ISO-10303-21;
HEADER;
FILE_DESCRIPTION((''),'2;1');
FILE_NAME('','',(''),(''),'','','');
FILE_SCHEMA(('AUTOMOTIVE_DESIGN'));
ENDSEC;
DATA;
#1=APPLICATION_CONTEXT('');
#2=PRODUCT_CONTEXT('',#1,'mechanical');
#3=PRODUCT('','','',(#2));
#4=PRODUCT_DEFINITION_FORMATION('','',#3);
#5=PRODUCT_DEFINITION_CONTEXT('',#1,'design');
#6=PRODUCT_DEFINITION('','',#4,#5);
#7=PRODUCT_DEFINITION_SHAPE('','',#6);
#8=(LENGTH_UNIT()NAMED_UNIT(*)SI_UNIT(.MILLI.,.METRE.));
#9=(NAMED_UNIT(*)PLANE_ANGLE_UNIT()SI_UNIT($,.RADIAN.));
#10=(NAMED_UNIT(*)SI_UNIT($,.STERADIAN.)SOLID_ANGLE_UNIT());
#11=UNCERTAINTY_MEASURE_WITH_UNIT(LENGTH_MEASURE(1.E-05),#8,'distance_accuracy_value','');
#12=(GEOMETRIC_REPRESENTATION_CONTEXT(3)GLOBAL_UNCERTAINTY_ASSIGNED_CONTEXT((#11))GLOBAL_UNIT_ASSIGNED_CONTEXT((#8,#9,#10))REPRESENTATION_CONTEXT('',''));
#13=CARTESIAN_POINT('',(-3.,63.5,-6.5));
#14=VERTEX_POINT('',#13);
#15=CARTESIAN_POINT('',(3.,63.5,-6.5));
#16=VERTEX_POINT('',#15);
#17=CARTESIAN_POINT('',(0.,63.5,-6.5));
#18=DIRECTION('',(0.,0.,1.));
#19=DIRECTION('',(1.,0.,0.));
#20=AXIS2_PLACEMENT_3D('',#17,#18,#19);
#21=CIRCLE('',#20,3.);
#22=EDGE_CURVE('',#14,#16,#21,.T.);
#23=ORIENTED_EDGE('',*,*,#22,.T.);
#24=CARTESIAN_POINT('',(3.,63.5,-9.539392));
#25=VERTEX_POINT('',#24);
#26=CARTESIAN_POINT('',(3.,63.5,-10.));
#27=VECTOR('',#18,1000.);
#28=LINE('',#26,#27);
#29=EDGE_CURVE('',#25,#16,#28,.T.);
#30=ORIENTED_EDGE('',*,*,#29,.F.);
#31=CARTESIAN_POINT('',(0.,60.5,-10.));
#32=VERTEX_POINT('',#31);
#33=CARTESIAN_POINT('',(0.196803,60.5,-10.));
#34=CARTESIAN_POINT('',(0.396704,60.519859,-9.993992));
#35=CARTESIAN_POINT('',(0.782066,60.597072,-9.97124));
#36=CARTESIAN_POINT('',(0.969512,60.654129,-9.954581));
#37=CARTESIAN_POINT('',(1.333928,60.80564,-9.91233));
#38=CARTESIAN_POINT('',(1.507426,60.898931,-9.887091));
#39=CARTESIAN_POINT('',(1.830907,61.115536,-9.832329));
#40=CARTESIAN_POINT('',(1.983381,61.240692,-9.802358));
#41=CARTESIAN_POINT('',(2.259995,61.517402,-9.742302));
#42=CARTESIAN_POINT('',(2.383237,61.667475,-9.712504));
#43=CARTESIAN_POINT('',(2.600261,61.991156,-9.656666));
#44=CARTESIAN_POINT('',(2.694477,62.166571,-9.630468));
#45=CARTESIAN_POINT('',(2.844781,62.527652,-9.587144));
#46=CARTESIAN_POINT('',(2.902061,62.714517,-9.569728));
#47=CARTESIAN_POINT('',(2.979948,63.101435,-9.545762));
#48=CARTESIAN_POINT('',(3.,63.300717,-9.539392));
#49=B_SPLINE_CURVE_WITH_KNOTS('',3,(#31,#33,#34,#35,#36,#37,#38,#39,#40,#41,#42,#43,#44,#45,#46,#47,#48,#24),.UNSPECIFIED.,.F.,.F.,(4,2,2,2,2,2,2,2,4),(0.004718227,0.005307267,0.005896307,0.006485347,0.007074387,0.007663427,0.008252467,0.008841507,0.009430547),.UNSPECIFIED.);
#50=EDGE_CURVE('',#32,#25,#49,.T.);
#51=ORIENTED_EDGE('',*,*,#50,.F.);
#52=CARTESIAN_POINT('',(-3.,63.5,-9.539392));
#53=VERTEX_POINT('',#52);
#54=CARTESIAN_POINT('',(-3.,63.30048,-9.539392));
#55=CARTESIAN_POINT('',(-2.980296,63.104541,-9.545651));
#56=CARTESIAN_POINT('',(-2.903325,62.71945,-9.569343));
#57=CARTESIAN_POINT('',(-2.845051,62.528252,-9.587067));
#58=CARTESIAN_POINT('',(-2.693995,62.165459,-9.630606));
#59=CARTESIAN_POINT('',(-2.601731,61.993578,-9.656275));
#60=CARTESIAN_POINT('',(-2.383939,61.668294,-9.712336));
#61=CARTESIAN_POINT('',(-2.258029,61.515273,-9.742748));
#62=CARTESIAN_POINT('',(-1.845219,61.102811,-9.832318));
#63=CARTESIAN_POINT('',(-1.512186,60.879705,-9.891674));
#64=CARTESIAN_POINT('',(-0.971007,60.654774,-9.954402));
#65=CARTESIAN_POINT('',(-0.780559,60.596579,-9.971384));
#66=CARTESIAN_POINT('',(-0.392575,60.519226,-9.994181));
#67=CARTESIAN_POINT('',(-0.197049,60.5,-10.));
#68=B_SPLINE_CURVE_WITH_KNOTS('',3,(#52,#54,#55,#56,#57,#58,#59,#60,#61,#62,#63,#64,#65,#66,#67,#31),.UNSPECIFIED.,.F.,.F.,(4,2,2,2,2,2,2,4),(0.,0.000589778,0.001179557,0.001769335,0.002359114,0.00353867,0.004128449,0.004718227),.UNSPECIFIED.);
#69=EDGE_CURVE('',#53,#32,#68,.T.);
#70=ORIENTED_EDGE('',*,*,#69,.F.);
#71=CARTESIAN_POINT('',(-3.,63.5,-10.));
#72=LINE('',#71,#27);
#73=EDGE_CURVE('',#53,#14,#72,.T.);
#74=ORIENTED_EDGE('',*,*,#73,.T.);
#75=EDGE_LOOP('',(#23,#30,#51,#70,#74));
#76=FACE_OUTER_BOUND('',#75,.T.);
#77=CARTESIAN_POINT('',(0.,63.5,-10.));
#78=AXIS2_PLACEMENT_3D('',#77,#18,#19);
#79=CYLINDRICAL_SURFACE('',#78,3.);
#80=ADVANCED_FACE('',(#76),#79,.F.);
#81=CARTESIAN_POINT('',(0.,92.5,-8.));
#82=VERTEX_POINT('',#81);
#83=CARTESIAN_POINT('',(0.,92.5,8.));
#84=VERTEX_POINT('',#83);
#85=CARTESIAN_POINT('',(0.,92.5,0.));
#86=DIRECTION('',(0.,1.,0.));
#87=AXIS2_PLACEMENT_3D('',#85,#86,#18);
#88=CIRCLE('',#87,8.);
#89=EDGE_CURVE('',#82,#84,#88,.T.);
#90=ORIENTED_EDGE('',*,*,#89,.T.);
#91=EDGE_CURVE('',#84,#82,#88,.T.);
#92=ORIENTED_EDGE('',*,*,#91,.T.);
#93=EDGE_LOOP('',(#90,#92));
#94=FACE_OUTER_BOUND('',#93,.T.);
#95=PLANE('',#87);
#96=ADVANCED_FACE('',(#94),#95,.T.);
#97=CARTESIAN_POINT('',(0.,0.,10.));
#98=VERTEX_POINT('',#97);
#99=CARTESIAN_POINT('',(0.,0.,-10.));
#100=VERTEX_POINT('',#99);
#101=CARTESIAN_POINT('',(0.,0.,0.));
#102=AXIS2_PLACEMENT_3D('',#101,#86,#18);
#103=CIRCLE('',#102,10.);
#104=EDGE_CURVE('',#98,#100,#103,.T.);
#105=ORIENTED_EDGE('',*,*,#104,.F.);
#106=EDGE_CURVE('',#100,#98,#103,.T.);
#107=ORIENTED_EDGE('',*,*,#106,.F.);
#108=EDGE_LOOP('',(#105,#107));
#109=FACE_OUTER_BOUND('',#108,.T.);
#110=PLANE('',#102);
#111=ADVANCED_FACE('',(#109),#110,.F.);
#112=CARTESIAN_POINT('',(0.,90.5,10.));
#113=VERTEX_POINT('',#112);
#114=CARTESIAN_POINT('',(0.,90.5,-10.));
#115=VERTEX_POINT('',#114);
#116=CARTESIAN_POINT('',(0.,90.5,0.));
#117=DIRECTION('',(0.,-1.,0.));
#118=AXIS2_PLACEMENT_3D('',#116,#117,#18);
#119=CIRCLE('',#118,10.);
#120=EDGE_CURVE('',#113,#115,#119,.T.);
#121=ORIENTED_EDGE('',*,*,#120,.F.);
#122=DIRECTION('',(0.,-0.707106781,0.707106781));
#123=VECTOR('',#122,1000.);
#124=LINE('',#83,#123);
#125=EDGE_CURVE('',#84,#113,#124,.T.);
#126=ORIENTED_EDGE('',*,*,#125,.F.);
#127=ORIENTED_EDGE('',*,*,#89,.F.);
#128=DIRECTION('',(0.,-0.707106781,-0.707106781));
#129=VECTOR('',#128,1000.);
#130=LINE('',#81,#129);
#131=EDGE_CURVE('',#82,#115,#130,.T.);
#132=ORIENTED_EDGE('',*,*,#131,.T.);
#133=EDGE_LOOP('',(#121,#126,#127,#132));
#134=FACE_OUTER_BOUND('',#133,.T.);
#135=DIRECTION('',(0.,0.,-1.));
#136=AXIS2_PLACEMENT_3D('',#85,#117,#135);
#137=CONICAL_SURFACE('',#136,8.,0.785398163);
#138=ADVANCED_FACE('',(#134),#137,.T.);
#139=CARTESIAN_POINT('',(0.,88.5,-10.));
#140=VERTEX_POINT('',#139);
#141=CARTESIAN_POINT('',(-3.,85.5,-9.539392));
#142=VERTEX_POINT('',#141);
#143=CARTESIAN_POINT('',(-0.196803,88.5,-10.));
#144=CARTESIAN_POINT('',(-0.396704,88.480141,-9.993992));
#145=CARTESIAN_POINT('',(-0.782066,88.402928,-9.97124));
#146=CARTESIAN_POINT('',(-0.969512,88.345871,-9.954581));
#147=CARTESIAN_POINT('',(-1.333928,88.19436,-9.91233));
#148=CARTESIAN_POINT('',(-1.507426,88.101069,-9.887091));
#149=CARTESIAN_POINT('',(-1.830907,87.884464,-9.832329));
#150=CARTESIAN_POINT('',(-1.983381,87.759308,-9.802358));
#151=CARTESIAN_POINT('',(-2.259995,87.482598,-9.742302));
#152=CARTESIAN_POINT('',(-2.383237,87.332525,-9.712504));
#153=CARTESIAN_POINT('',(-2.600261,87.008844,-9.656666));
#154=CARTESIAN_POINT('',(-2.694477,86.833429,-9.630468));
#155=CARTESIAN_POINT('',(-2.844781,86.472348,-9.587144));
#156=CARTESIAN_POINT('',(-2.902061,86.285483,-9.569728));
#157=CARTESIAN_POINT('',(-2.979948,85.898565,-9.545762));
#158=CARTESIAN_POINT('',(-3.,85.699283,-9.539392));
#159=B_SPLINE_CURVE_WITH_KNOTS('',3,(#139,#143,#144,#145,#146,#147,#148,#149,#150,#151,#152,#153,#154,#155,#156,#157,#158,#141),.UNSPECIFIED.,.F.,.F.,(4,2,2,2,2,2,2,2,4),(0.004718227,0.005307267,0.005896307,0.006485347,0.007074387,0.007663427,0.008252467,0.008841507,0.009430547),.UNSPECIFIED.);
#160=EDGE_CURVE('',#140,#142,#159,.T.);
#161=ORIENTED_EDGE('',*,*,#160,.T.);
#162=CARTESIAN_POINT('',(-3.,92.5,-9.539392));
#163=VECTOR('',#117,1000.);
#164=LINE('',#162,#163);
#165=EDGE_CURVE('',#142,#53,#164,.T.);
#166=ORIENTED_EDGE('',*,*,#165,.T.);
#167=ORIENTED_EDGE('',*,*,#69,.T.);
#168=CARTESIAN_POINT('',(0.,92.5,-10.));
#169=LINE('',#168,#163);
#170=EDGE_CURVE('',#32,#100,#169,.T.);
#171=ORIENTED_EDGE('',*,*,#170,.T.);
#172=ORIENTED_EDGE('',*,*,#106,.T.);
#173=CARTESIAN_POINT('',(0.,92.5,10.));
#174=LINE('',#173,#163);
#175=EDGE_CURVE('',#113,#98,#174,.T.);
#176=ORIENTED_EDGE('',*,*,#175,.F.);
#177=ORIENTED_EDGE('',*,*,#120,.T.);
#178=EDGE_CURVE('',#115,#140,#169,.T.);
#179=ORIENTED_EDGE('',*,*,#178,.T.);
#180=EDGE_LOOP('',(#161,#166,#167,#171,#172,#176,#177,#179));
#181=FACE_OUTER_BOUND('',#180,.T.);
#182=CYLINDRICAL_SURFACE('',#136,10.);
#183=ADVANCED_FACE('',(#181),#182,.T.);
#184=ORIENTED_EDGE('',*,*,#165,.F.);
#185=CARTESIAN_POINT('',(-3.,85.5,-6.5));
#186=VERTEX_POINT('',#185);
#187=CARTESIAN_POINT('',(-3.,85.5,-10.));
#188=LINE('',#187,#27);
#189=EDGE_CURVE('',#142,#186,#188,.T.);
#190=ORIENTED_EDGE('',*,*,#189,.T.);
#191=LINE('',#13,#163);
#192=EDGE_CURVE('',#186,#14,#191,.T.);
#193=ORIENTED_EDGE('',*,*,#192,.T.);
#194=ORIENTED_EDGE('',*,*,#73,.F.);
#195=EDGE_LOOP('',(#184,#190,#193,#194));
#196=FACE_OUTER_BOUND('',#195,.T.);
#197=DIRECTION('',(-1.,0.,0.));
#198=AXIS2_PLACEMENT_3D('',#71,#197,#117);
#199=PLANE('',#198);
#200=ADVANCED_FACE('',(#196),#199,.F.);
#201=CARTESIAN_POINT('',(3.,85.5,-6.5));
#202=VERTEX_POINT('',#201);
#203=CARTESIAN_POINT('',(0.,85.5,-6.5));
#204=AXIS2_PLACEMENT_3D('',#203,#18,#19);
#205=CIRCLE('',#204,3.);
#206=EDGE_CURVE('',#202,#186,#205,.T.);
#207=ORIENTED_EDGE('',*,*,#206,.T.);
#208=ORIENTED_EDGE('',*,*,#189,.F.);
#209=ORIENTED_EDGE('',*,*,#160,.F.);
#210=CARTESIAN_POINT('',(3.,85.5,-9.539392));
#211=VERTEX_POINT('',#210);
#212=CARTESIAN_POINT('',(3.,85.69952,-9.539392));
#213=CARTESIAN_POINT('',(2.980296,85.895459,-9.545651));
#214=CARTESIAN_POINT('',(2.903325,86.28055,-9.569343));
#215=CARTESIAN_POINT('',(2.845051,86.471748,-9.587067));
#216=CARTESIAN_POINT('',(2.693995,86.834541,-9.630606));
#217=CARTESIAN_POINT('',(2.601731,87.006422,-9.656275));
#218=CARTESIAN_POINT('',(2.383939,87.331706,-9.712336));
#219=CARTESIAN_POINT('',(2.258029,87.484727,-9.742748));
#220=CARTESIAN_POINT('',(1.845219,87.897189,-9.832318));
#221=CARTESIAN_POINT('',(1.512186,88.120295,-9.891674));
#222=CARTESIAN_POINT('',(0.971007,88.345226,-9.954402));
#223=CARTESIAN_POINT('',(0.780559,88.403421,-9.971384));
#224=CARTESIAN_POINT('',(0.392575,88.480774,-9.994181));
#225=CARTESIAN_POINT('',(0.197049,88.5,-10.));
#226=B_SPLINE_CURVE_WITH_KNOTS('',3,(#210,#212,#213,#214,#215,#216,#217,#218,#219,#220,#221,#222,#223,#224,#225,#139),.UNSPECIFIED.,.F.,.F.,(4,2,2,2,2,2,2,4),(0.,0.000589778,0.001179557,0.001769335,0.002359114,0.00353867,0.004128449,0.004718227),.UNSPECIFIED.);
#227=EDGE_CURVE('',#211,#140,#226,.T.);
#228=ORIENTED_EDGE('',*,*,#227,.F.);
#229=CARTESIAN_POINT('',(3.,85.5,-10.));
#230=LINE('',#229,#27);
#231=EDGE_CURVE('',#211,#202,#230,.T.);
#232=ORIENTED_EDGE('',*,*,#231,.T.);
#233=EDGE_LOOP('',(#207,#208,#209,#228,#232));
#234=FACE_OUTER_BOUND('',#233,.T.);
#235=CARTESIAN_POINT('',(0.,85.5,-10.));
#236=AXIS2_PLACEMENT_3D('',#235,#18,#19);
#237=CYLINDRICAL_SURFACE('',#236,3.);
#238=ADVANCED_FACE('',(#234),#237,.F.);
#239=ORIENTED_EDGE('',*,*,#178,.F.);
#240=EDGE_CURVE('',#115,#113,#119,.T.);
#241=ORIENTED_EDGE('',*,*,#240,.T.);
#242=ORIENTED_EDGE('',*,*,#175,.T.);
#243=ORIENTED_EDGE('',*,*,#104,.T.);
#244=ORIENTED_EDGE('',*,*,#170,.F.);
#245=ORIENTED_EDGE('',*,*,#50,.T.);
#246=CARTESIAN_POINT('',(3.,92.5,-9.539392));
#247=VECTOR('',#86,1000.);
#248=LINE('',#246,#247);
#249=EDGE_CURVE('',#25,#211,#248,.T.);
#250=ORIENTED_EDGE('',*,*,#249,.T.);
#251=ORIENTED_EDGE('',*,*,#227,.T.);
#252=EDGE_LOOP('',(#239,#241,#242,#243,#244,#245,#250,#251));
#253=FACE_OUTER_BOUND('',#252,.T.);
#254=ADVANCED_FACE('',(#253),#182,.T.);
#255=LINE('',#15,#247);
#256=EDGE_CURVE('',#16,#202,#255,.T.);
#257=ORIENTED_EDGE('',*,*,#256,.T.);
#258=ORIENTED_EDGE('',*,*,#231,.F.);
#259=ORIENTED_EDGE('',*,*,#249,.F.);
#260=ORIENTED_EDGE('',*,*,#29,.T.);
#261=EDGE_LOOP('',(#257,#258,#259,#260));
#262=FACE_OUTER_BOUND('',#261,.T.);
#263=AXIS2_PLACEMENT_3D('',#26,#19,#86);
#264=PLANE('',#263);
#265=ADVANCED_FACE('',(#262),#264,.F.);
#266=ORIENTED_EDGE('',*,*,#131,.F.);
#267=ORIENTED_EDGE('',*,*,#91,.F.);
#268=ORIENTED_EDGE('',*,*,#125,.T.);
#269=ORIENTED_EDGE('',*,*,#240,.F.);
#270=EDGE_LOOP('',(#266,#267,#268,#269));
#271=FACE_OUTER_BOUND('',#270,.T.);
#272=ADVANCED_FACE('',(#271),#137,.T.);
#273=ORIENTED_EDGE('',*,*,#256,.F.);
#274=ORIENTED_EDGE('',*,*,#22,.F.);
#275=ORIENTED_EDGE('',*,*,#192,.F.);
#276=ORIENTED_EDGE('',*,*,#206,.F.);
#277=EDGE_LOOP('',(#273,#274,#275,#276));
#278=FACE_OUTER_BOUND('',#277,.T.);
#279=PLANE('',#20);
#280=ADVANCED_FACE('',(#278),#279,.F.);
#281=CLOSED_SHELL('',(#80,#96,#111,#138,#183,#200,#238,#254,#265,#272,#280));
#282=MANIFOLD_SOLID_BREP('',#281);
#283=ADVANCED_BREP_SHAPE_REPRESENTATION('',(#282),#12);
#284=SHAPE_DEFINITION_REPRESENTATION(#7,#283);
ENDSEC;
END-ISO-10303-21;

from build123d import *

# Parameters (mm, degrees)
SKETCH_1_R           = 10
BOSS_EXTRUDE_1_DEPTH = 92.5
CUT_EXTRUDE_1_DEPTH  = 95.490740287
CHAMFER_1_SIZE       = 2


with BuildPart() as part:
    # Sketch 1 → Boss-Extrude 1 (new body)
    with BuildSketch(Plane(origin=(0, 0, 0), x_dir=(1, 0, 0), z_dir=(0, 1, 0))):
        with Locations(Location((0, 0, 0), (0, 0, 270))):
            Circle(SKETCH_1_R)
    extrude(amount=BOSS_EXTRUDE_1_DEPTH)

    # Sketch 2 → Cut-Extrude 1 (cut, through all)
    with BuildSketch(Plane.XY.offset(-6.5)):
        with BuildLine():
            Line((-3, 63.5), (-3, 85.5))
            ThreePointArc((-3, 85.5), (0, 88.5), (3, 85.5))
            Line((3, 85.5), (3, 63.5))
            ThreePointArc((3, 63.5), (0, 60.5), (-3, 63.5))
        make_face()
    extrude(amount=-CUT_EXTRUDE_1_DEPTH, mode=Mode.SUBTRACT)

    # Chamfer 1
    chamfer_1_edges = [part.edges().sort_by_distance(p)[0] for p in [
        (0, 92.5, -10),
    ]]
    chamfer(chamfer_1_edges, length=CHAMFER_1_SIZE)


solid = part.part
